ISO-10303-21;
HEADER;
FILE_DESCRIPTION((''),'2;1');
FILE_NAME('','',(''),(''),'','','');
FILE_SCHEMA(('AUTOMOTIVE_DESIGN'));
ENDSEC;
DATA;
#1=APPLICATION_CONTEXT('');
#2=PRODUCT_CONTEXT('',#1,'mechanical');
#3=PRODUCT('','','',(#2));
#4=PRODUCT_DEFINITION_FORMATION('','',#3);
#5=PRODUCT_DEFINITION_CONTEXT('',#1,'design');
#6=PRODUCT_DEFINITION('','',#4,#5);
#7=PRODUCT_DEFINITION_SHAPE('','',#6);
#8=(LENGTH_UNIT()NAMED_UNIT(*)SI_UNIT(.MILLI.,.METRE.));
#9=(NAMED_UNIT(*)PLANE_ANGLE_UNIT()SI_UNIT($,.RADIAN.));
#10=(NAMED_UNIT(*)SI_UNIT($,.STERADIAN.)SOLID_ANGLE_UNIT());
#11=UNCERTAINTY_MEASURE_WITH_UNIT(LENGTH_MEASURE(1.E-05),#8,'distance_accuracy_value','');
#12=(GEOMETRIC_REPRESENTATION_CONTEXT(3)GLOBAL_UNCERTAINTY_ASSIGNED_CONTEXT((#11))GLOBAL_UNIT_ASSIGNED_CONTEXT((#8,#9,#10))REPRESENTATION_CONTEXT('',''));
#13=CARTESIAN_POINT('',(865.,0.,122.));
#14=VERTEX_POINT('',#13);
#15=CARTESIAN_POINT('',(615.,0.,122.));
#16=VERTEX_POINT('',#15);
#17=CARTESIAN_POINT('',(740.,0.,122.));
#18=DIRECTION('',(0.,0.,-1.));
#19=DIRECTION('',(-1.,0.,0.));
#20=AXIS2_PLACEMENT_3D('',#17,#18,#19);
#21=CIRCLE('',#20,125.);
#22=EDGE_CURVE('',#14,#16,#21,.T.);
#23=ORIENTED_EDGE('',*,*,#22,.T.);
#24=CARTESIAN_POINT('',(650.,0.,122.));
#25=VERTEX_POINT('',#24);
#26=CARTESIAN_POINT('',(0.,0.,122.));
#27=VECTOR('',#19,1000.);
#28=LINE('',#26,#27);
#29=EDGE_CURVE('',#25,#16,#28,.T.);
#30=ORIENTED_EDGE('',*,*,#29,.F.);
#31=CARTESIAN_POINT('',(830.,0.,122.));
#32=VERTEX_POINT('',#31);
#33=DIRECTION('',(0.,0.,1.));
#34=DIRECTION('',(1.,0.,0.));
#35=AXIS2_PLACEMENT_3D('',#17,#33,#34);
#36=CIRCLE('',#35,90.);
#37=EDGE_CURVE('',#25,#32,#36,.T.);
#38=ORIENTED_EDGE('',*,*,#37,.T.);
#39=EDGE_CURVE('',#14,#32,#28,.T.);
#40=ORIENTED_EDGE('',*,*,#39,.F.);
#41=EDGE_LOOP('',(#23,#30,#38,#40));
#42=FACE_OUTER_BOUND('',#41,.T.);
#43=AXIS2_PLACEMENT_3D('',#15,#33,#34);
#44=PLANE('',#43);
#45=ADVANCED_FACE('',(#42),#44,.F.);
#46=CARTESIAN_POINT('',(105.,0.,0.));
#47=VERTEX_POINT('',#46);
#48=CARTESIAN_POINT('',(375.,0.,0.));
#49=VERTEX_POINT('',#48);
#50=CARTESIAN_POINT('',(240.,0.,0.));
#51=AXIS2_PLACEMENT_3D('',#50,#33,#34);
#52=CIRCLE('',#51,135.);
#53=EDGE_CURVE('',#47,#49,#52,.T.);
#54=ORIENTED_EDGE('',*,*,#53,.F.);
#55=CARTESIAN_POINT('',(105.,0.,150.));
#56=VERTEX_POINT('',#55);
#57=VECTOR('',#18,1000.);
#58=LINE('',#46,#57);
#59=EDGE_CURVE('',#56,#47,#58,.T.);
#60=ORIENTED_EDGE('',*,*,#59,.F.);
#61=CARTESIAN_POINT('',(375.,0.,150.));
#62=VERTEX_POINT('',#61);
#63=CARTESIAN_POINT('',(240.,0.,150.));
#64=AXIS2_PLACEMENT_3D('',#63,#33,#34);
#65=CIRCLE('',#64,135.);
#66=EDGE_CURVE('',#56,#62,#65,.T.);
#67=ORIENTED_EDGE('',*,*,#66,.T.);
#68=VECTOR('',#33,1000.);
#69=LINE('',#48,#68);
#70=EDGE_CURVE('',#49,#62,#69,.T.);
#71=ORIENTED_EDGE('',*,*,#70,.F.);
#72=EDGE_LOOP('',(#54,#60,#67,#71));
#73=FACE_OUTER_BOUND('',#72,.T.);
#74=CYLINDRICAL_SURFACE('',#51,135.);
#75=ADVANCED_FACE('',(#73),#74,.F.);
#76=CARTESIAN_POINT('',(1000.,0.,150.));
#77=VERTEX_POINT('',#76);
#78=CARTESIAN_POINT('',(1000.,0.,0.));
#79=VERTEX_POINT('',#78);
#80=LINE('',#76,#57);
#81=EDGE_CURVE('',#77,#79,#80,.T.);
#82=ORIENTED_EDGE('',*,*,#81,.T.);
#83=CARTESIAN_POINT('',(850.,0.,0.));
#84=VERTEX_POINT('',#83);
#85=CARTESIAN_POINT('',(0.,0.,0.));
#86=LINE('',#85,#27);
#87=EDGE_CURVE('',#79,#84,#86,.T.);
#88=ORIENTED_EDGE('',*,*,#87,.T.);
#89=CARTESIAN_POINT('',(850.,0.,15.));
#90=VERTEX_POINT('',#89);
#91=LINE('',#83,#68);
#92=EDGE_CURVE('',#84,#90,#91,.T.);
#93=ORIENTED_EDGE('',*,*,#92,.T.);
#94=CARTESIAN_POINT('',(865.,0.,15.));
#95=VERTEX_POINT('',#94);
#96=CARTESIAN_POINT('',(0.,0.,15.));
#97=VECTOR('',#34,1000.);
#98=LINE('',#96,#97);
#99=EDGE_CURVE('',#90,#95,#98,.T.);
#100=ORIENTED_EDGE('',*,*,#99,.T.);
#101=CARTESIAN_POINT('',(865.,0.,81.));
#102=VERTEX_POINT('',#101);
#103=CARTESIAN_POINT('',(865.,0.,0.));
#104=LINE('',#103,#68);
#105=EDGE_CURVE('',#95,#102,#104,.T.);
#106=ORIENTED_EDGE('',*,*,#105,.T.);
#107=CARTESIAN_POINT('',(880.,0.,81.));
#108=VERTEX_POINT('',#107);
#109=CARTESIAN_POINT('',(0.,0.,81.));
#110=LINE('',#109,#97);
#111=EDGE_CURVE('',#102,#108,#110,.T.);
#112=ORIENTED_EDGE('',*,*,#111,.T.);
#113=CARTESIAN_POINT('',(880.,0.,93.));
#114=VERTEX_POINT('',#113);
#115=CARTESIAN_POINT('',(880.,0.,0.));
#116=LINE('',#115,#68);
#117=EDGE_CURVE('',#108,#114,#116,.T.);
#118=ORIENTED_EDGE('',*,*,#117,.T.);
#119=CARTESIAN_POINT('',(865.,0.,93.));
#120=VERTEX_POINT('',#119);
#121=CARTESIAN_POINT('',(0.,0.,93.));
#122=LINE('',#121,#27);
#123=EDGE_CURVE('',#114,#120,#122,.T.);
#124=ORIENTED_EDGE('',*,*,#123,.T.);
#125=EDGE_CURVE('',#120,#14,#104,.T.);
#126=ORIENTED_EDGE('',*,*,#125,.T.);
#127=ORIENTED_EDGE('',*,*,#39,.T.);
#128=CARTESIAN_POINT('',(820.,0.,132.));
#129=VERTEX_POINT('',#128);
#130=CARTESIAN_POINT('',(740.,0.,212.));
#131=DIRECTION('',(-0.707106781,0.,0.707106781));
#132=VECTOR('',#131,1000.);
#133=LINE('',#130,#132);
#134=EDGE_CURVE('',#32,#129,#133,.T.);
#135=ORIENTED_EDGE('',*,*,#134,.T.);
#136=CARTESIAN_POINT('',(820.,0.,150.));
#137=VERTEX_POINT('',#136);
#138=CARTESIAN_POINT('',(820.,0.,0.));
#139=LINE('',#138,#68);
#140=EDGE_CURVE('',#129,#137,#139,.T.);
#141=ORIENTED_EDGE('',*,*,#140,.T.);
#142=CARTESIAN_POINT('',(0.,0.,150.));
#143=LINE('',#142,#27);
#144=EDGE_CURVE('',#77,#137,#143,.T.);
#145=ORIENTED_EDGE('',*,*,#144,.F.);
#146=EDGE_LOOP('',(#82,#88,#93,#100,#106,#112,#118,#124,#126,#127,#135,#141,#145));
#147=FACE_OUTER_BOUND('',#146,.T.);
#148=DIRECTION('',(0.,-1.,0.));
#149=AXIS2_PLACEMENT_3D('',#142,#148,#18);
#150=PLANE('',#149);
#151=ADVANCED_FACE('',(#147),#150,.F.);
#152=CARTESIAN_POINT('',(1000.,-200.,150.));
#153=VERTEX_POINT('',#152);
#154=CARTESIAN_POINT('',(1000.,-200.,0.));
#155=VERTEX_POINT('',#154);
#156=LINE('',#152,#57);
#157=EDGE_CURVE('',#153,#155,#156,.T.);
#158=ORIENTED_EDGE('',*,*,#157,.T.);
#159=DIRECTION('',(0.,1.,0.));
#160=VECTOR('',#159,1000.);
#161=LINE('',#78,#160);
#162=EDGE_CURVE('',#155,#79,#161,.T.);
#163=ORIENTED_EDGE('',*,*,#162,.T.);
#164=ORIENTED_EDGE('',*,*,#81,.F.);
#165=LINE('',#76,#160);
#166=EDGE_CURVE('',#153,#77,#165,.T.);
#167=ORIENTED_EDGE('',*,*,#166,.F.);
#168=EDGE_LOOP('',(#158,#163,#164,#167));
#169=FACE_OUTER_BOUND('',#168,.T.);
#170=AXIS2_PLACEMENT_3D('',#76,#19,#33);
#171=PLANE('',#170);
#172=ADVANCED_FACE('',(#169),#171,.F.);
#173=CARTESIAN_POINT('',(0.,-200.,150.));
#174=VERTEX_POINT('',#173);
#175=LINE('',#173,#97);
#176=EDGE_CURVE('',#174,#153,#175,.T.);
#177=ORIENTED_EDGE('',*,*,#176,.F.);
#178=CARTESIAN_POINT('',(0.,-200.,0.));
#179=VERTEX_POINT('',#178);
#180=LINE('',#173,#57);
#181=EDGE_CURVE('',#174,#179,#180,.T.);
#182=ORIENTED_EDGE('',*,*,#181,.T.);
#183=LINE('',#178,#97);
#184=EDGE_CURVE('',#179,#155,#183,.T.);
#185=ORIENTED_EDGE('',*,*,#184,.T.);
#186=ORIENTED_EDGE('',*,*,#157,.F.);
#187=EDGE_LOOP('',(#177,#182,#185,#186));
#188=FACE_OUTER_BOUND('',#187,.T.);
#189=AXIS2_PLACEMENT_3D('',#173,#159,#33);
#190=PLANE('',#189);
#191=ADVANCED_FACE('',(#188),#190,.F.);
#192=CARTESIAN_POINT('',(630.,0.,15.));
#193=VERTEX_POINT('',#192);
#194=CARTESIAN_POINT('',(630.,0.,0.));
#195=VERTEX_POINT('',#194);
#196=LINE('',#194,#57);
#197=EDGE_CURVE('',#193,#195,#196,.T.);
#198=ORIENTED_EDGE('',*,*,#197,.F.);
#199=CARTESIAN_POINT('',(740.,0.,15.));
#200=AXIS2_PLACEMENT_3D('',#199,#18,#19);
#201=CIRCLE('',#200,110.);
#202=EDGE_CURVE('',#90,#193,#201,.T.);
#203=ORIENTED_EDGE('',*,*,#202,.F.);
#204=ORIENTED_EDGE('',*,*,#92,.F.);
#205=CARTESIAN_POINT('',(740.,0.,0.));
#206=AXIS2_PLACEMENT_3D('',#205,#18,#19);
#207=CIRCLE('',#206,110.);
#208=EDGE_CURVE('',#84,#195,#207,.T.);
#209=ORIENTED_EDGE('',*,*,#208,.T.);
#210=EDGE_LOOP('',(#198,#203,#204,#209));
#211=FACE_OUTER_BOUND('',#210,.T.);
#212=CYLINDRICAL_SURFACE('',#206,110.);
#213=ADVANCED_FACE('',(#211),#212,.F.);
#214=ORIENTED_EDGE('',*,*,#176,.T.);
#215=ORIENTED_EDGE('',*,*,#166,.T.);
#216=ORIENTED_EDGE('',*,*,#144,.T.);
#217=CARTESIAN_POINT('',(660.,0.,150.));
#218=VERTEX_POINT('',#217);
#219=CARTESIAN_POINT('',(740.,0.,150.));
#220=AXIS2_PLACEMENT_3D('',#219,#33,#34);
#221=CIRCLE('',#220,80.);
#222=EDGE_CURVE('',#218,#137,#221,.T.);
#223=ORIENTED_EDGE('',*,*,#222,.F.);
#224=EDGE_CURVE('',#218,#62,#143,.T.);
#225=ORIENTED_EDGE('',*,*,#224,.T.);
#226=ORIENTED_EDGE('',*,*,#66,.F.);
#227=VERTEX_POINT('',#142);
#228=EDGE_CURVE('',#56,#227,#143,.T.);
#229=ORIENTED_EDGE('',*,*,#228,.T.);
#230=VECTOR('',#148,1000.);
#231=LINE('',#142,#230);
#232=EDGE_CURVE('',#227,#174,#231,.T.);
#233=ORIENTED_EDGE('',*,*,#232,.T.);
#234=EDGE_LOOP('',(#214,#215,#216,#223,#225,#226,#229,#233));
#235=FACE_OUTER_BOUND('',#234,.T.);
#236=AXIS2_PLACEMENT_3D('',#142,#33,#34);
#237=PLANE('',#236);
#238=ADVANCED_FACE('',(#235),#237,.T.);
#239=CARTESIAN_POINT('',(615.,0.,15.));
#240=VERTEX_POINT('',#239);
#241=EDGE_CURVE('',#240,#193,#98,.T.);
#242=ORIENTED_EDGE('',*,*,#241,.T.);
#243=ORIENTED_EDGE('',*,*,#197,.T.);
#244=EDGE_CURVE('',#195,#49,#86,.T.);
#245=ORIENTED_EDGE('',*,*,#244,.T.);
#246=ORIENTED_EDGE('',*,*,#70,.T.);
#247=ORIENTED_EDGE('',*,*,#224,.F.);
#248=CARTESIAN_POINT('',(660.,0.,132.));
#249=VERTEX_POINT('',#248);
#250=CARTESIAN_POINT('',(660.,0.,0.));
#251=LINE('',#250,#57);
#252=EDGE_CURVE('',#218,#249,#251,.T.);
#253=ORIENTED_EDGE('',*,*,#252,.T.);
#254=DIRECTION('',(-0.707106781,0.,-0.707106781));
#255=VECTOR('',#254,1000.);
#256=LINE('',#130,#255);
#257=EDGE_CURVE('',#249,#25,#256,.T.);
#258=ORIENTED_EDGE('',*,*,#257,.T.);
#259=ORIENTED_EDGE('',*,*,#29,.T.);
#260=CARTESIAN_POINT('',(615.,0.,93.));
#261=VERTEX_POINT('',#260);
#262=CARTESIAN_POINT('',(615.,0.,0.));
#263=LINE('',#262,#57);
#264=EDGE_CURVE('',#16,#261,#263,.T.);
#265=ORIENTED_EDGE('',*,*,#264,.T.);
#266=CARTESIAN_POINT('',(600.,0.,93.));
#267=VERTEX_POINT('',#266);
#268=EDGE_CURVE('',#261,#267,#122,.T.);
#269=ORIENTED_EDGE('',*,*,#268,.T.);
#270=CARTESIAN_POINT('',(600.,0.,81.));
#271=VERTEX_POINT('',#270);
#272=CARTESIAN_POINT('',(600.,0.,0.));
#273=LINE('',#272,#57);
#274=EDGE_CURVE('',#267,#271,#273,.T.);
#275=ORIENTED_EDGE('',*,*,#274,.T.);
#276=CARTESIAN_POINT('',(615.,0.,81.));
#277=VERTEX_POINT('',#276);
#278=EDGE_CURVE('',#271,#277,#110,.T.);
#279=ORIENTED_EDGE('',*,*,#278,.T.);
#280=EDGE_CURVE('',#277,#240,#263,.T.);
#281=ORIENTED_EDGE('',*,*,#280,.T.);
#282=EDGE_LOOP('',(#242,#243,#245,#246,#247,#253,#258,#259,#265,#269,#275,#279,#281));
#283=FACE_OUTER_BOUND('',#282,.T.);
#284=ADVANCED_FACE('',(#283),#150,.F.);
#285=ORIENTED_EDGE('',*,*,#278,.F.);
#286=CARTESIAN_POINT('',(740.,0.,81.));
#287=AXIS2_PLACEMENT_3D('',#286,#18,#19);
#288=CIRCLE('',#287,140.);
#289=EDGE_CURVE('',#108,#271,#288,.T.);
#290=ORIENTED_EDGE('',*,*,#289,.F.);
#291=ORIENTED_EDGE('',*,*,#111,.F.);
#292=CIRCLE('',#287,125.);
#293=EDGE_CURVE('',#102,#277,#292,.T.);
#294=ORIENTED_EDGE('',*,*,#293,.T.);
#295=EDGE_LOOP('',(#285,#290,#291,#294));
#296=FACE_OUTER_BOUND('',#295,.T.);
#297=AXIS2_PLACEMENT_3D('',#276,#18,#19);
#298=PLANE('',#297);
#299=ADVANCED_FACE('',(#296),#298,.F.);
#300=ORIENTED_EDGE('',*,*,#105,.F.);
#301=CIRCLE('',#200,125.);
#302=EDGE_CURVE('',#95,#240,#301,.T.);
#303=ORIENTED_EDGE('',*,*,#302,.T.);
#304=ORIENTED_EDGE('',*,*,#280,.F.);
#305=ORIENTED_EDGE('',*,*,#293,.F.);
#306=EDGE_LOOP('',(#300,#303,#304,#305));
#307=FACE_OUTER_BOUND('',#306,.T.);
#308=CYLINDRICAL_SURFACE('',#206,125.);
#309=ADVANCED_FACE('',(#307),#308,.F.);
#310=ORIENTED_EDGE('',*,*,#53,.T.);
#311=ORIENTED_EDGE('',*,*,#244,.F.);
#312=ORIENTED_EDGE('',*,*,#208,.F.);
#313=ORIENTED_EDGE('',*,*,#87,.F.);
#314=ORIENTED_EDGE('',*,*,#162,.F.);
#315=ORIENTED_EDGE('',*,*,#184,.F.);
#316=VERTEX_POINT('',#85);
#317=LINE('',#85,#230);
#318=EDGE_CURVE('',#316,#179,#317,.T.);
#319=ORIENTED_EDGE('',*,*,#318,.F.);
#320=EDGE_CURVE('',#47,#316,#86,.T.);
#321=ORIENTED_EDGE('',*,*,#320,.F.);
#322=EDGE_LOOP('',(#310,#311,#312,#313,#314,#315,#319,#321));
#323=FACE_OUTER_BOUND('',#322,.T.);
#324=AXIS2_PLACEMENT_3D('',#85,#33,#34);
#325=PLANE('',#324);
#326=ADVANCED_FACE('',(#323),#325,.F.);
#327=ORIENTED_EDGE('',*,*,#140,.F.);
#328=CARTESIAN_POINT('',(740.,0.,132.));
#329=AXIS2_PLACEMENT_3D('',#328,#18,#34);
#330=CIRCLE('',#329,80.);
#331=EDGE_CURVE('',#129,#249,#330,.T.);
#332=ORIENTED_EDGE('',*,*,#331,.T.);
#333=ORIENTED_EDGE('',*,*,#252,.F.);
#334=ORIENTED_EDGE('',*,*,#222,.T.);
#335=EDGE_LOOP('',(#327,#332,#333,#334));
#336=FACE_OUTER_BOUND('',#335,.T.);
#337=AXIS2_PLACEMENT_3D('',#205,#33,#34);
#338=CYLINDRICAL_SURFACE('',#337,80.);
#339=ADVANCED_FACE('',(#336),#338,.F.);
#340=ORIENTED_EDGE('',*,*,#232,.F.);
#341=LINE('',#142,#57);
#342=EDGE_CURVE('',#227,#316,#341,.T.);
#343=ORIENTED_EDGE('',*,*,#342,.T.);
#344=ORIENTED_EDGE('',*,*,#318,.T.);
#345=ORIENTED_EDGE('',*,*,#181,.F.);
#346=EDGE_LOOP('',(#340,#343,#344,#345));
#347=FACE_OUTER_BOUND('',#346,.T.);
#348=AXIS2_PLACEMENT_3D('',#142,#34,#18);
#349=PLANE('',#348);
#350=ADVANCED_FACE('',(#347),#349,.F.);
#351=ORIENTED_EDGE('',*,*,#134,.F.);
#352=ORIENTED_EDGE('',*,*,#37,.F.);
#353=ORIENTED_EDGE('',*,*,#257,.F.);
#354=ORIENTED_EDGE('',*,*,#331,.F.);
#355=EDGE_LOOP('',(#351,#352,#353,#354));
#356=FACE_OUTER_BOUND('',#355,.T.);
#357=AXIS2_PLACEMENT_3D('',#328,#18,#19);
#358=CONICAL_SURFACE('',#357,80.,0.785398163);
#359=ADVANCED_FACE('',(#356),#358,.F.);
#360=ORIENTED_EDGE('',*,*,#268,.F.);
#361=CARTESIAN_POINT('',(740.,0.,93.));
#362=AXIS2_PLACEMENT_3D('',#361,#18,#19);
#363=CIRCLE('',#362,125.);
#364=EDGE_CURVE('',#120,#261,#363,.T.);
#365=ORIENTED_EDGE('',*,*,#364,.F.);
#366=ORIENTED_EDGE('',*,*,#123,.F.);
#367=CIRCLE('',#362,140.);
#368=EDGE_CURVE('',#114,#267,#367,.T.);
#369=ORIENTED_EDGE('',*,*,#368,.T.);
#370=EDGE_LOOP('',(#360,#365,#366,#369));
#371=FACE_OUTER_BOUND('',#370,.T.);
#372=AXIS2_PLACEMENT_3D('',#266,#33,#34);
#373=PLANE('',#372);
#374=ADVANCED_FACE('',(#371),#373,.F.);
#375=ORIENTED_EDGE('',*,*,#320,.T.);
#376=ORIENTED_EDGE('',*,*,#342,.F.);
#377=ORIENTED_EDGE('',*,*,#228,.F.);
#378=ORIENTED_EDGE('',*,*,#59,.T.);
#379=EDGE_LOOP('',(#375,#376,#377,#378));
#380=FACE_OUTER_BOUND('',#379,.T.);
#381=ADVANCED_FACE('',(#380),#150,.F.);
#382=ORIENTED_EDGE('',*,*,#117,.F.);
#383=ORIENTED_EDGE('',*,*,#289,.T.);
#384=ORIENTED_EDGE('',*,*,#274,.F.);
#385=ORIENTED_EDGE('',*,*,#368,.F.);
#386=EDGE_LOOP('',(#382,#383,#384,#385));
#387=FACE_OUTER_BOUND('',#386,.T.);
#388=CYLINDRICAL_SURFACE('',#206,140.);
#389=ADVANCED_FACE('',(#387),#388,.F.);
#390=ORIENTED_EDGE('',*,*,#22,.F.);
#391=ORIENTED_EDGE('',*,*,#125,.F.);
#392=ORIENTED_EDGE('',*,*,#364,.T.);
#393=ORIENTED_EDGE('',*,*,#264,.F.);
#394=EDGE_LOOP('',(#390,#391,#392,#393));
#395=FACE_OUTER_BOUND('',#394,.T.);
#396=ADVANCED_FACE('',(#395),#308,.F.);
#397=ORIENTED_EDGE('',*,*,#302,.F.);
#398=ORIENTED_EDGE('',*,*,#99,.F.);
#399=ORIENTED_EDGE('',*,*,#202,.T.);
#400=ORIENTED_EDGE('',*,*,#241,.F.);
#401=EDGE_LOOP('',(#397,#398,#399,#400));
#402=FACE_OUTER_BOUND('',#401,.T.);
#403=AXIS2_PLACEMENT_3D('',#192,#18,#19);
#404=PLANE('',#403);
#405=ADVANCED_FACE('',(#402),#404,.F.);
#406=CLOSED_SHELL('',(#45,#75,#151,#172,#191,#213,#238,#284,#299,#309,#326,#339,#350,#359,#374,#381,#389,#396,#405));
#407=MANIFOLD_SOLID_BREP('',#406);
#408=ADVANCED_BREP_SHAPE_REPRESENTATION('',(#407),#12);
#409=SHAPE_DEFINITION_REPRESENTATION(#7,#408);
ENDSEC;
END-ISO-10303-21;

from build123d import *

# Parameters (mm, degrees)
SKETCH1_W               = 1000
SKETCH1_H               = 200
BOSS_EXTRUDE1_DEPTH     = 150
CUT_EXTRUDE1_DEPTH      = 1031.776406404
CUT_EXTRUDE1_DEPTH_BACK = 1031.776406404
SKETCH2_R               = 135
SKETCH2_R_2             = 80
CHAMFER1_SIZE           = 10


with BuildPart() as part:
    # Sketch1 → Boss-Extrude1 (new body)
    with BuildSketch(Plane.XY):
        with Locations((500, -100)):
            Rectangle(SKETCH1_W, SKETCH1_H)
    extrude(amount=BOSS_EXTRUDE1_DEPTH)

    # Sketch2 → Cut-Extrude1 (cut, two sides: drawn at the far end of the back side and taken through both)
    with BuildSketch(Plane.XY.offset(150).offset(-CUT_EXTRUDE1_DEPTH_BACK)):
        with Locations((240, 0)):
            Circle(SKETCH2_R)
        with Locations((740, 0)):
            Circle(SKETCH2_R_2)
    extrude(amount=CUT_EXTRUDE1_DEPTH + CUT_EXTRUDE1_DEPTH_BACK, mode=Mode.SUBTRACT)

    # Sketch3 → Cut-Revolve1 (revolve, cut)
    with BuildSketch(Plane(origin=(0, 0, 0), x_dir=(1, 0, 0), z_dir=(0, 1, 0))):
        Polygon((740, -150), (660, -150), (660, -122), (615, -122), (615, -93), (600, -93), (600, -81), (615, -81), (615, -15), (630, -15), (630, 0), (740, 0), align=None)
    revolve(axis=Axis((740, 0, 0), (0, 0, 1)), mode=Mode.SUBTRACT)

    # Chamfer1
    chamfer1_edges = [part.edges().sort_by_distance(p)[0] for p in [
        (740, -80, 122),
    ]]
    chamfer(chamfer1_edges, length=CHAMFER1_SIZE)


solid = part.part
